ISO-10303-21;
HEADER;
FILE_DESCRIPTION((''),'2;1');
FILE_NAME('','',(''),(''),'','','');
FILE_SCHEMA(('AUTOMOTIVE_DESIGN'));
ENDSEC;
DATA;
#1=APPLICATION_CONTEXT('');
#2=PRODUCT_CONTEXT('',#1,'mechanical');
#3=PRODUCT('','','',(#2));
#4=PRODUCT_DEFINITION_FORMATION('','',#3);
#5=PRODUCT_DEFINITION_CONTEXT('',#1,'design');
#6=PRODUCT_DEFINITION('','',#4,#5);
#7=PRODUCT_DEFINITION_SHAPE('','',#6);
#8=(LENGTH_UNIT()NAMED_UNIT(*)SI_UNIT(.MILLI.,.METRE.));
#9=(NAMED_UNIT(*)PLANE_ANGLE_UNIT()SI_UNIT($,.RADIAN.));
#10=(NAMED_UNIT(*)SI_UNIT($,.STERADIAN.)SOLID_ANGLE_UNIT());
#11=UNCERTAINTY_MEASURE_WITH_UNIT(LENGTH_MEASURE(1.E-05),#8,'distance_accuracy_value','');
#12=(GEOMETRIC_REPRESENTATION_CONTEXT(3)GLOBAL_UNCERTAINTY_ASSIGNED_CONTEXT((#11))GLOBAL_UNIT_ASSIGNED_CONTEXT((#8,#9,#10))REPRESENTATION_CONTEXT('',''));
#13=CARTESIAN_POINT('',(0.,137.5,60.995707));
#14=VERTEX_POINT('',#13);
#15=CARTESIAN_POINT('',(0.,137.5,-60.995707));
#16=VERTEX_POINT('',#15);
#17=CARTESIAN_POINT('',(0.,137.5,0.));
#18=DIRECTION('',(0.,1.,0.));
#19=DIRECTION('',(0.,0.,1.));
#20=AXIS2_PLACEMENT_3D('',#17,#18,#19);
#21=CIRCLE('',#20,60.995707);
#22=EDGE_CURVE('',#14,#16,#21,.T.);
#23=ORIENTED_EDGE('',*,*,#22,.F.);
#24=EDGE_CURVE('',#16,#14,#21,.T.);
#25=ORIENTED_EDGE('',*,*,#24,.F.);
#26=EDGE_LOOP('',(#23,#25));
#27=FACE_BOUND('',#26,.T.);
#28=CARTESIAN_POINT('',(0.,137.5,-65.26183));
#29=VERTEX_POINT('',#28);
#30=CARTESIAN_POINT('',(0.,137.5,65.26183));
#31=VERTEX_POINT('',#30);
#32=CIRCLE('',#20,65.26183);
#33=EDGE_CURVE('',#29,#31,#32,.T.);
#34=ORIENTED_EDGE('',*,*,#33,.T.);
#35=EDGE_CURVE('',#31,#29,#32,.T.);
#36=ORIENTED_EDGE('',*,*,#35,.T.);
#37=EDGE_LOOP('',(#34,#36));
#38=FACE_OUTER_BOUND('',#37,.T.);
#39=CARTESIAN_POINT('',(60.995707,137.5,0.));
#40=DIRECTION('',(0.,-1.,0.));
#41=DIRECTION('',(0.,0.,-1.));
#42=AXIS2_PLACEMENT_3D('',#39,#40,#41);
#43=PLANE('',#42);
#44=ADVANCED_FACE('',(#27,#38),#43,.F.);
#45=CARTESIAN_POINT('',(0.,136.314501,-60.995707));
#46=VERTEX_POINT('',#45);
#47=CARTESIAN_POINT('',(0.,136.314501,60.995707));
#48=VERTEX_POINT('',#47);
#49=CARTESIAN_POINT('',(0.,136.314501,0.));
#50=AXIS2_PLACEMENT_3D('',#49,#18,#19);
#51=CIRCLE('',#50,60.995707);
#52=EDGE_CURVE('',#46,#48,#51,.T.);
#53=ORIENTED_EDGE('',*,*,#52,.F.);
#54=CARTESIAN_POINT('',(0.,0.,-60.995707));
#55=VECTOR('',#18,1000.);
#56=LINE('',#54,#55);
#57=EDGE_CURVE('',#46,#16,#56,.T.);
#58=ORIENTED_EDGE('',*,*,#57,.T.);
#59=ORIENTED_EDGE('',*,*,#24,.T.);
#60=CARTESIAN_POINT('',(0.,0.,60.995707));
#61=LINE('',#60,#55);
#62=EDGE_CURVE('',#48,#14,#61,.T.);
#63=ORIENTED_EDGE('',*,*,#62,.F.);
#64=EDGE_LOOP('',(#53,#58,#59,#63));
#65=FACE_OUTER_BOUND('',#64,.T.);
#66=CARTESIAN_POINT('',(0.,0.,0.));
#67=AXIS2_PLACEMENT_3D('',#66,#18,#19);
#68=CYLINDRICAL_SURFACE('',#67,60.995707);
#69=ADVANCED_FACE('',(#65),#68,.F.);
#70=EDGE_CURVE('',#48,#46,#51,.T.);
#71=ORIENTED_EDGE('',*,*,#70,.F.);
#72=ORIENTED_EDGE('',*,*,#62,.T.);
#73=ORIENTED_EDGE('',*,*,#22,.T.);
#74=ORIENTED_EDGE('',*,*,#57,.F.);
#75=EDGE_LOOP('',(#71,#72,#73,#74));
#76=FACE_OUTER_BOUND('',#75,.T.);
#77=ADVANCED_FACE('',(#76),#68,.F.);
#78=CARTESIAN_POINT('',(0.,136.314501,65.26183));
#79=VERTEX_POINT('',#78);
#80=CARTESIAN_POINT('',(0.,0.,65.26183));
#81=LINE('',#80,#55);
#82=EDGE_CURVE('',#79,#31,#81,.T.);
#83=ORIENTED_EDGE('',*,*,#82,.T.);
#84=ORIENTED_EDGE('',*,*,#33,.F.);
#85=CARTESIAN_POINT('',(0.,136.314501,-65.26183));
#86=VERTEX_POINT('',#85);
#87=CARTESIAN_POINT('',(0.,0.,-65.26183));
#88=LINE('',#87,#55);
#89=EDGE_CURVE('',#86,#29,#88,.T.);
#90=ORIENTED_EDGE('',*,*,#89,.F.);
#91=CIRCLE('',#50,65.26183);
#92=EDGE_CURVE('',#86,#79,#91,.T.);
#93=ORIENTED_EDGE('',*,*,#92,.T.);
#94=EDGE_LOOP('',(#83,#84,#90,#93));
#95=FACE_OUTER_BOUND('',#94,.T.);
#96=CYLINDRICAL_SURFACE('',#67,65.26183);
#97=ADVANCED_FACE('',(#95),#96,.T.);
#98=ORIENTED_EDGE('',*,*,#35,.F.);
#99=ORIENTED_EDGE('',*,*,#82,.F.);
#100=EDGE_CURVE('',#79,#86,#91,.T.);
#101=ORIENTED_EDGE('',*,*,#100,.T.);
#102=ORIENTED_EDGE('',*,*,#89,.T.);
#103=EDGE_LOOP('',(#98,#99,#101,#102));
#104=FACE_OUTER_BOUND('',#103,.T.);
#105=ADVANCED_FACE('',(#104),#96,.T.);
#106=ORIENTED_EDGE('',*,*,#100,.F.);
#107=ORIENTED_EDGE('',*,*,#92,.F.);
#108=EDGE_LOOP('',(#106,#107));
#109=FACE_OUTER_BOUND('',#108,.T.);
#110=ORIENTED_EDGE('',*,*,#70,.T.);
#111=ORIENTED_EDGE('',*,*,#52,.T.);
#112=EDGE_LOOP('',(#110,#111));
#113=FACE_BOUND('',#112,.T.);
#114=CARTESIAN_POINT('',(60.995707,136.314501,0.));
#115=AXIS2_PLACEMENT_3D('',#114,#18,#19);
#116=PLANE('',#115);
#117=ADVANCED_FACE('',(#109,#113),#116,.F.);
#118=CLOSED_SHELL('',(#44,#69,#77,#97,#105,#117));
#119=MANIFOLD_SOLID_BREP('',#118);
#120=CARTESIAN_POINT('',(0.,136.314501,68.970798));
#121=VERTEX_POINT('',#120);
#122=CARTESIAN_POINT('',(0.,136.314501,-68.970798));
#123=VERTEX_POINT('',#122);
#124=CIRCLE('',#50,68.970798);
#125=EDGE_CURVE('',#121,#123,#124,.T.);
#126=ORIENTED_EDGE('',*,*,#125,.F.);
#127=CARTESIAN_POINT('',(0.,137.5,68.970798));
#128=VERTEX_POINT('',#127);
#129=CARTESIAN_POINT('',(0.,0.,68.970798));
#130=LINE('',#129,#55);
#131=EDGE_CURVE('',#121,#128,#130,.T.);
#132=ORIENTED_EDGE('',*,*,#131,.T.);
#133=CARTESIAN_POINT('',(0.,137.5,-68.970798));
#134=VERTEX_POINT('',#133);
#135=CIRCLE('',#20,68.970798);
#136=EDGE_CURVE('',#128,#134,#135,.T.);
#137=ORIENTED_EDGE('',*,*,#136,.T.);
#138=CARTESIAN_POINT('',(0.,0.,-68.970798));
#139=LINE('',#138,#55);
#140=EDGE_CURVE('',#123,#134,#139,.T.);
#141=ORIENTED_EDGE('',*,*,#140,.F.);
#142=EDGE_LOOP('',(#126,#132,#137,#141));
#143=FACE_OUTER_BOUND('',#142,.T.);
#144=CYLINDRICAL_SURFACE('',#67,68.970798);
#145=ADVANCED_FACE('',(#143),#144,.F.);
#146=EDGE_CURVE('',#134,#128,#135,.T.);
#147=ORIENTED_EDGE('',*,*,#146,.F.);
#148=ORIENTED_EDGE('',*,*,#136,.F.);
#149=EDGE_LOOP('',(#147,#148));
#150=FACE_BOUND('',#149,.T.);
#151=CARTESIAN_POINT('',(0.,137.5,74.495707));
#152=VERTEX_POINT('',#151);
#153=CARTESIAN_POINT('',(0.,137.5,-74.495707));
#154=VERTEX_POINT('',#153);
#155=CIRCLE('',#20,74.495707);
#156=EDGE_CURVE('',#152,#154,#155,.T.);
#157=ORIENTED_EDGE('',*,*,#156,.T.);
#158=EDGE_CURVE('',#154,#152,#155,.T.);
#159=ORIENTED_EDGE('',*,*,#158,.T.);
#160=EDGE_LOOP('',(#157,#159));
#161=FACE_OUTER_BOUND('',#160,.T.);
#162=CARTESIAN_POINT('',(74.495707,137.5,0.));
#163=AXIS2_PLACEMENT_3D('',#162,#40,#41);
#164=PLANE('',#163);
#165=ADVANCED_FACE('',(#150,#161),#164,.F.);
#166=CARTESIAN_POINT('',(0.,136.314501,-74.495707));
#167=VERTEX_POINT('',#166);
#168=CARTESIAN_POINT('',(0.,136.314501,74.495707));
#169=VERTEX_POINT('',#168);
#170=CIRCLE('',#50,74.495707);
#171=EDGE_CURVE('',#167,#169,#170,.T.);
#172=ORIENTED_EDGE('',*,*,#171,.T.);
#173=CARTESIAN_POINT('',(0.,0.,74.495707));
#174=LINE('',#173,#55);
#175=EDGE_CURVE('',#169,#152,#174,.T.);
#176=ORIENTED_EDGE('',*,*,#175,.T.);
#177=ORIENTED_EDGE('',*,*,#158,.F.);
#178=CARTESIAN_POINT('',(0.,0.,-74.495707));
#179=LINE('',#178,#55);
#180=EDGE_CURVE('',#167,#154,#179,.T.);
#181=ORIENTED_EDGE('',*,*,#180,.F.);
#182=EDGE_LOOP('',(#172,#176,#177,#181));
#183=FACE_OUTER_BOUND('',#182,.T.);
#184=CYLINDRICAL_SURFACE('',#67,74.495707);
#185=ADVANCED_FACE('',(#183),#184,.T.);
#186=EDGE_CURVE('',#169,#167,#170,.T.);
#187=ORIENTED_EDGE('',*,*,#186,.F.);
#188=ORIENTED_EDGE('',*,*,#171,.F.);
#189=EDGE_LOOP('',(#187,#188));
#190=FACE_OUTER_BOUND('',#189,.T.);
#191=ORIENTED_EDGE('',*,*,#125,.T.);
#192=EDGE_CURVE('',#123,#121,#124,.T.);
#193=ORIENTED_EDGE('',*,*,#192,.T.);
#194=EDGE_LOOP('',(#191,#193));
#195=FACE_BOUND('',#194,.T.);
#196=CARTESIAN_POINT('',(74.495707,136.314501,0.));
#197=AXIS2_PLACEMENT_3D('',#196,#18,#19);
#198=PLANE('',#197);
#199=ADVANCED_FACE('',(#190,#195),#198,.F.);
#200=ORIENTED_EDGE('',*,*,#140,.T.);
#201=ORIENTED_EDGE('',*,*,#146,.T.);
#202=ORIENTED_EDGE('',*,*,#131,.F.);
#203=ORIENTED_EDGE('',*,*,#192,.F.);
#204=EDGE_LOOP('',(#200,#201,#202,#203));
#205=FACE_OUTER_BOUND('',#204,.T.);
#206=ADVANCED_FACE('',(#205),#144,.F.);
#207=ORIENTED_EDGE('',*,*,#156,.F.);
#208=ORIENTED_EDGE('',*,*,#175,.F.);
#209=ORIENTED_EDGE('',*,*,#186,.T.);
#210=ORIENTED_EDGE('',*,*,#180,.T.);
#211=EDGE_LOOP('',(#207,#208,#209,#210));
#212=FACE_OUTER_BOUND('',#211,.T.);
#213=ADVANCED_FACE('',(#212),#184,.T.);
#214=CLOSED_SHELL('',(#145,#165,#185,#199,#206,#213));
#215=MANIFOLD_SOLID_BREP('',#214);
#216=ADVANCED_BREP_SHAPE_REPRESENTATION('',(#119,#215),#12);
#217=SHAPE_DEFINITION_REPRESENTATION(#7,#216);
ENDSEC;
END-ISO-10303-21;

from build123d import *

# Parameters (mm, degrees)
SKETCH1_W   = 5.524909439
SKETCH1_H   = 1.185499442
SKETCH1_W_2 = 4.266122689


with BuildPart() as part:
    # Sketch1 → Revolve1 (revolve)
    with BuildSketch(Plane.XY, mode=Mode.PRIVATE) as revolve1_sk:
        with Locations((71.733252241, 136.907250279)):
            Rectangle(SKETCH1_W, SKETCH1_H)
        with Locations((63.128768306, 136.907250279)):
            Rectangle(SKETCH1_W_2, SKETCH1_H)
    revolve(revolve1_sk.sketch.rotate(Axis((0, 0, 0), (0, -1, 0)), 90), axis=Axis((0, 0, 0), (0, -1, 0)))


solid = part.part
